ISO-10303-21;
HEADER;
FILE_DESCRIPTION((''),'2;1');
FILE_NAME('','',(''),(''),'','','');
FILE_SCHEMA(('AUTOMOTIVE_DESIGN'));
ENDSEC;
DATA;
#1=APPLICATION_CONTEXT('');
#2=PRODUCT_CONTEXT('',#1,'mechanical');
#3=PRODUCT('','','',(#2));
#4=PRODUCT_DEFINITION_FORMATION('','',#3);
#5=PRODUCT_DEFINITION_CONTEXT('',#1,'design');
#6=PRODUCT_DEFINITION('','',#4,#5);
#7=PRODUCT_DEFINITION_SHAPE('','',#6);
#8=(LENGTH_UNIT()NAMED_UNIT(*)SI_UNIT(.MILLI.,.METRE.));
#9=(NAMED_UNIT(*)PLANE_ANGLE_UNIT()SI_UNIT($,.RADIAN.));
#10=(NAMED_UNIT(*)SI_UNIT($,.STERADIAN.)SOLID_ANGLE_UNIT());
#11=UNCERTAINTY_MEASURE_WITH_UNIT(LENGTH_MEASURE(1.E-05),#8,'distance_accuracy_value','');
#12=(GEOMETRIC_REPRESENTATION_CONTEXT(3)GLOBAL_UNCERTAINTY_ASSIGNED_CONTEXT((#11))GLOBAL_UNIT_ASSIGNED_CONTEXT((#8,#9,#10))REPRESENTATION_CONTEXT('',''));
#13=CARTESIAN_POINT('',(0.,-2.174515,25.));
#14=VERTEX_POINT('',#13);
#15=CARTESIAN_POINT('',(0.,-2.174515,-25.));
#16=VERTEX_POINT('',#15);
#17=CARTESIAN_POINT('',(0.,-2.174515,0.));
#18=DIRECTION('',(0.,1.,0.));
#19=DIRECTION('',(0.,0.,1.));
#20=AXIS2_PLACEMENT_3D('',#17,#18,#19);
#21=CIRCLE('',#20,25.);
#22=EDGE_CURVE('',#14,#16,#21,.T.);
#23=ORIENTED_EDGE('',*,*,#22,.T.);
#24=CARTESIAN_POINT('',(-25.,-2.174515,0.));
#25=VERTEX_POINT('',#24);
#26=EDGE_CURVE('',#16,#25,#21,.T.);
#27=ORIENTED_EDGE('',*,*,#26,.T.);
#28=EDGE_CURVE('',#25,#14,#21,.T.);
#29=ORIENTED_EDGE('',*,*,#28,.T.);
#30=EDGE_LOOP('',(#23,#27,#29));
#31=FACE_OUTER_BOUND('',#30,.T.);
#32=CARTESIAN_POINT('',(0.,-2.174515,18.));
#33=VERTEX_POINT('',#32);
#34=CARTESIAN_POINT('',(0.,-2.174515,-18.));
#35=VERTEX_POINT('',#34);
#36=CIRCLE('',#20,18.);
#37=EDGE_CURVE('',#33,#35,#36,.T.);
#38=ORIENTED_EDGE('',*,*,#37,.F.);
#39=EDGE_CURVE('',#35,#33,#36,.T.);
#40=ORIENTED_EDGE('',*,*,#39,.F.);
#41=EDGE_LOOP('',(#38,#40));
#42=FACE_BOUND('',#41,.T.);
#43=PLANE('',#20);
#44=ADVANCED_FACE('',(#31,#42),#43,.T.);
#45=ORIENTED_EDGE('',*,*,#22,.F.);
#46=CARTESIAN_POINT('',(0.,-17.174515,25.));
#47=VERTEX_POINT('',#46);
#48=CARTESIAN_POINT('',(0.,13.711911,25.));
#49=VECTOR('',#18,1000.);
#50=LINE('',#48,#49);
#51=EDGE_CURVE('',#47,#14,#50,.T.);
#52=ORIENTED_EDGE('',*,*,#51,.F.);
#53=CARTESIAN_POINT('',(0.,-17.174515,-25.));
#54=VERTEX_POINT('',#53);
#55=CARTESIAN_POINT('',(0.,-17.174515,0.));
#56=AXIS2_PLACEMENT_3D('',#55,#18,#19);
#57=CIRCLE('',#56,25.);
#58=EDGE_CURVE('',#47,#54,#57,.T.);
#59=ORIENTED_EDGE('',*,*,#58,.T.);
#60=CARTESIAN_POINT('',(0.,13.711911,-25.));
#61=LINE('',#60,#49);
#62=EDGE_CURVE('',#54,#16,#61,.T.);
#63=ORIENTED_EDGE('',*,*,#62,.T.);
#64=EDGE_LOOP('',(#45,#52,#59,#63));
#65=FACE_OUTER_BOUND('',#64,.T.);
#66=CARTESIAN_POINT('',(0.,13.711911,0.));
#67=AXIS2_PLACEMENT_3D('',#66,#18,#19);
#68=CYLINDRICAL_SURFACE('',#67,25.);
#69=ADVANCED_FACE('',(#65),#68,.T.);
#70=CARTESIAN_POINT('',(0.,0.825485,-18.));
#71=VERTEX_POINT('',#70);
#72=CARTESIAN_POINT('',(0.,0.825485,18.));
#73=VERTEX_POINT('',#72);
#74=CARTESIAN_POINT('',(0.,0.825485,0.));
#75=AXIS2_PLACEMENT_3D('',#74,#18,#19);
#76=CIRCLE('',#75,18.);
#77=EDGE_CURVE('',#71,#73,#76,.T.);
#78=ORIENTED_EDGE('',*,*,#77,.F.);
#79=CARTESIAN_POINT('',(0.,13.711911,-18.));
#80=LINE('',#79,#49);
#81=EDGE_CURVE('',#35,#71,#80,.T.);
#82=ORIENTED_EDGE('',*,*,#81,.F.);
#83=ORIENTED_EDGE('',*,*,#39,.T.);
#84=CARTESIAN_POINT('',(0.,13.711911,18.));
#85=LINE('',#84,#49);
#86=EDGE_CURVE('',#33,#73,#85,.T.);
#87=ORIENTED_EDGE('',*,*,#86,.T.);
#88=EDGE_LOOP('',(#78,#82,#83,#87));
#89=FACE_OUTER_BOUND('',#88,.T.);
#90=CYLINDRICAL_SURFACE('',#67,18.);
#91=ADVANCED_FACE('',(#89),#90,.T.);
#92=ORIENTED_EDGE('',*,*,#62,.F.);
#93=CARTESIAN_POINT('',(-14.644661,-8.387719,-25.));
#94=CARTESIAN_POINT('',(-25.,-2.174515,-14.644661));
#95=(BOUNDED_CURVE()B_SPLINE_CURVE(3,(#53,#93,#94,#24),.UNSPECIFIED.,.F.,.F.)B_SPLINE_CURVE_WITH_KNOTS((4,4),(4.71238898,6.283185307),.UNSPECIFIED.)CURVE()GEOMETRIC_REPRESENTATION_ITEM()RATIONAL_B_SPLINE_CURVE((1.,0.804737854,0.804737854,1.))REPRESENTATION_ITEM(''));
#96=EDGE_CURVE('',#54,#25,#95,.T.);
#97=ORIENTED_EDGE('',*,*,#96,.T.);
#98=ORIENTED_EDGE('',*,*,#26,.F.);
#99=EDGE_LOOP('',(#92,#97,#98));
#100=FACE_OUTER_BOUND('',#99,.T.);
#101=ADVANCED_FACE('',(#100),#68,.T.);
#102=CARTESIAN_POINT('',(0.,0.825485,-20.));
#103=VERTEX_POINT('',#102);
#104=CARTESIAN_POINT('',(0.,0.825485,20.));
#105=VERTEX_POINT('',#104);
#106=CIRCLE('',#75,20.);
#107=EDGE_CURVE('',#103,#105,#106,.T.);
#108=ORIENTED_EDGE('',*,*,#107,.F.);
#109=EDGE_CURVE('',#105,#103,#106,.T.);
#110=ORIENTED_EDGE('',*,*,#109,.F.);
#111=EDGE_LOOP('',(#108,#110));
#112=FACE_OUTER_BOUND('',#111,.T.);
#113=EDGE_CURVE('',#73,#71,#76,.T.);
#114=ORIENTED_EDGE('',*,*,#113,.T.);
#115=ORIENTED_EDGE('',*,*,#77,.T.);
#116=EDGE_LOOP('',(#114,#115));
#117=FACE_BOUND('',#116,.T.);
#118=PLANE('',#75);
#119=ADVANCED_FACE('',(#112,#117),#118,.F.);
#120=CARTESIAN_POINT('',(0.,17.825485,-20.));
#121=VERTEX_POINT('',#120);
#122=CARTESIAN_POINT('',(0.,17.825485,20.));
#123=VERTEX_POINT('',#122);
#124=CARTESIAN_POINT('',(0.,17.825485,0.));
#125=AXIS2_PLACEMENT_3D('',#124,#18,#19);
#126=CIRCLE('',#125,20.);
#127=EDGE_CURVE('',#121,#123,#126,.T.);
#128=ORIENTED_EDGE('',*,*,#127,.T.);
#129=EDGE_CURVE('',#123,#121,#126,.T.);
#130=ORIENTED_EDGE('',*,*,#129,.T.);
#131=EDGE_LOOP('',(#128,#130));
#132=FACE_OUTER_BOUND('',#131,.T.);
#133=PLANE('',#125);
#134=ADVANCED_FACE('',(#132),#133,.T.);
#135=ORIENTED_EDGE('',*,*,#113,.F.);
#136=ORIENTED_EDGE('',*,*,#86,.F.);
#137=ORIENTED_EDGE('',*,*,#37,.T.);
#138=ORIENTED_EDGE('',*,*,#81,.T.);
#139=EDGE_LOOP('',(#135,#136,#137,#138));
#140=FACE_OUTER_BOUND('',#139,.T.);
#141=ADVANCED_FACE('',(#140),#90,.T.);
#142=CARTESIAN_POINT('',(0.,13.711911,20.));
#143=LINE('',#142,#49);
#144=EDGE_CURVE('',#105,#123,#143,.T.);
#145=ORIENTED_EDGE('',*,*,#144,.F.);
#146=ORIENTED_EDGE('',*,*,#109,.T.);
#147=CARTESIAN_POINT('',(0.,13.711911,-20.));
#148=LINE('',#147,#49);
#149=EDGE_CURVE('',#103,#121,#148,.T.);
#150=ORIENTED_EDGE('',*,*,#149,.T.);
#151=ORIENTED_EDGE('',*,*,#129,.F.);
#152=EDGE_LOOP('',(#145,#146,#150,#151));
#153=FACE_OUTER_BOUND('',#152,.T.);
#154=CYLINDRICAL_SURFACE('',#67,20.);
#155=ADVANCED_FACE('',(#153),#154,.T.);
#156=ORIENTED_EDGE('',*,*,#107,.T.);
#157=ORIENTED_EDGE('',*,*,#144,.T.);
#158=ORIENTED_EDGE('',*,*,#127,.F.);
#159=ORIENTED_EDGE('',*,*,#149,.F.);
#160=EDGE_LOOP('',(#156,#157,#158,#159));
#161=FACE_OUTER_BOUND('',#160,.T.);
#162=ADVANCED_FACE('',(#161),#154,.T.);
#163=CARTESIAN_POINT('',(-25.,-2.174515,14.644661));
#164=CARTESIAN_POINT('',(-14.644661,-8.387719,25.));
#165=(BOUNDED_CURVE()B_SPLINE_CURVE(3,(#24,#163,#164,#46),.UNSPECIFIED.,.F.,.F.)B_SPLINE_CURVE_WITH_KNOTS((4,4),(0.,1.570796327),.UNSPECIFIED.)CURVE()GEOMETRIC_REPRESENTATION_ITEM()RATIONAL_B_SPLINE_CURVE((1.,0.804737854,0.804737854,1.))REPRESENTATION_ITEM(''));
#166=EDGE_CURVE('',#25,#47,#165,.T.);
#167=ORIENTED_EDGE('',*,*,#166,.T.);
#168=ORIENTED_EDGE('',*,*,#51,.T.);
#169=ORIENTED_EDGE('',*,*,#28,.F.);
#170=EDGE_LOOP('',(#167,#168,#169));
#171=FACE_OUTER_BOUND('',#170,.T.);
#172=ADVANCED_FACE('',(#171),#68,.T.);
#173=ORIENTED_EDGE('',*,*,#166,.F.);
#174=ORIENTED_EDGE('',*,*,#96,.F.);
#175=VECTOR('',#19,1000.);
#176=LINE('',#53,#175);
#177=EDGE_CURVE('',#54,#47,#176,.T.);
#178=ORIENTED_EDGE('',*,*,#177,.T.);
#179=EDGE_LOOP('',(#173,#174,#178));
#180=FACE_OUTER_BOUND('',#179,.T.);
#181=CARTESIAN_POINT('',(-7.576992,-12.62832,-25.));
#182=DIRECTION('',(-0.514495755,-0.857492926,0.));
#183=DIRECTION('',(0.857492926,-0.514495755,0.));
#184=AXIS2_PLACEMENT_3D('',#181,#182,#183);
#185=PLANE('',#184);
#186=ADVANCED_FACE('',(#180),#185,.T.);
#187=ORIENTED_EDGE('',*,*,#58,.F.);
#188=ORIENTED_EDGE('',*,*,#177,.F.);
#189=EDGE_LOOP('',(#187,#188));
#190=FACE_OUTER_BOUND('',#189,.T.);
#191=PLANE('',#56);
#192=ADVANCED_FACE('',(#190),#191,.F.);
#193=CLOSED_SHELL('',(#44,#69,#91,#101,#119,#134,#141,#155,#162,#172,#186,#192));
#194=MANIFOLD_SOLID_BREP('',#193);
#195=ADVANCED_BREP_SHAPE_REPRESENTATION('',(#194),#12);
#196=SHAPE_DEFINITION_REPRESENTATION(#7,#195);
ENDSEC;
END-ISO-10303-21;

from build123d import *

# Parameters (mm, degrees)
SKETCH1_W               = 20
SKETCH1_H               = 17
SKETCH1_W_2             = 18
SKETCH1_H_2             = 3
CUT_EXTRUDE1_DEPTH      = 40.594796465
CUT_EXTRUDE1_DEPTH_BACK = 40.594796465


with BuildPart() as part:
    # Sketch1 → Revolve2 (revolve)
    with BuildSketch(Plane.XY, mode=Mode.PRIVATE) as revolve2_sk:
        with Locations((-10, 9.325484765)):
            Rectangle(SKETCH1_W, SKETCH1_H)
        with Locations((-9, -0.674515235)):
            Rectangle(SKETCH1_W_2, SKETCH1_H_2)
        Polygon((0, -17.174515235), (0, -2.174515235), (-18, -2.174515235), (-25, -2.174515235), (-25, -17.174515235), align=None)
    revolve(revolve2_sk.sketch.rotate(Axis((0, 13.711911357, 0), (0, -1, 0)), 270), axis=Axis((0, 13.711911357, 0), (0, -1, 0)))

    # Sketch3 → Cut-Extrude1 (cut, two sides: drawn at the far end of the back side and taken through both)
    with BuildSketch(Plane.XY.offset(-CUT_EXTRUDE1_DEPTH_BACK)):
        Polygon((-25, -2.174515235), (0, -17.174515235), (-25, -17.174515235), align=None)
    extrude(amount=CUT_EXTRUDE1_DEPTH + CUT_EXTRUDE1_DEPTH_BACK, mode=Mode.SUBTRACT)


solid = part.part
